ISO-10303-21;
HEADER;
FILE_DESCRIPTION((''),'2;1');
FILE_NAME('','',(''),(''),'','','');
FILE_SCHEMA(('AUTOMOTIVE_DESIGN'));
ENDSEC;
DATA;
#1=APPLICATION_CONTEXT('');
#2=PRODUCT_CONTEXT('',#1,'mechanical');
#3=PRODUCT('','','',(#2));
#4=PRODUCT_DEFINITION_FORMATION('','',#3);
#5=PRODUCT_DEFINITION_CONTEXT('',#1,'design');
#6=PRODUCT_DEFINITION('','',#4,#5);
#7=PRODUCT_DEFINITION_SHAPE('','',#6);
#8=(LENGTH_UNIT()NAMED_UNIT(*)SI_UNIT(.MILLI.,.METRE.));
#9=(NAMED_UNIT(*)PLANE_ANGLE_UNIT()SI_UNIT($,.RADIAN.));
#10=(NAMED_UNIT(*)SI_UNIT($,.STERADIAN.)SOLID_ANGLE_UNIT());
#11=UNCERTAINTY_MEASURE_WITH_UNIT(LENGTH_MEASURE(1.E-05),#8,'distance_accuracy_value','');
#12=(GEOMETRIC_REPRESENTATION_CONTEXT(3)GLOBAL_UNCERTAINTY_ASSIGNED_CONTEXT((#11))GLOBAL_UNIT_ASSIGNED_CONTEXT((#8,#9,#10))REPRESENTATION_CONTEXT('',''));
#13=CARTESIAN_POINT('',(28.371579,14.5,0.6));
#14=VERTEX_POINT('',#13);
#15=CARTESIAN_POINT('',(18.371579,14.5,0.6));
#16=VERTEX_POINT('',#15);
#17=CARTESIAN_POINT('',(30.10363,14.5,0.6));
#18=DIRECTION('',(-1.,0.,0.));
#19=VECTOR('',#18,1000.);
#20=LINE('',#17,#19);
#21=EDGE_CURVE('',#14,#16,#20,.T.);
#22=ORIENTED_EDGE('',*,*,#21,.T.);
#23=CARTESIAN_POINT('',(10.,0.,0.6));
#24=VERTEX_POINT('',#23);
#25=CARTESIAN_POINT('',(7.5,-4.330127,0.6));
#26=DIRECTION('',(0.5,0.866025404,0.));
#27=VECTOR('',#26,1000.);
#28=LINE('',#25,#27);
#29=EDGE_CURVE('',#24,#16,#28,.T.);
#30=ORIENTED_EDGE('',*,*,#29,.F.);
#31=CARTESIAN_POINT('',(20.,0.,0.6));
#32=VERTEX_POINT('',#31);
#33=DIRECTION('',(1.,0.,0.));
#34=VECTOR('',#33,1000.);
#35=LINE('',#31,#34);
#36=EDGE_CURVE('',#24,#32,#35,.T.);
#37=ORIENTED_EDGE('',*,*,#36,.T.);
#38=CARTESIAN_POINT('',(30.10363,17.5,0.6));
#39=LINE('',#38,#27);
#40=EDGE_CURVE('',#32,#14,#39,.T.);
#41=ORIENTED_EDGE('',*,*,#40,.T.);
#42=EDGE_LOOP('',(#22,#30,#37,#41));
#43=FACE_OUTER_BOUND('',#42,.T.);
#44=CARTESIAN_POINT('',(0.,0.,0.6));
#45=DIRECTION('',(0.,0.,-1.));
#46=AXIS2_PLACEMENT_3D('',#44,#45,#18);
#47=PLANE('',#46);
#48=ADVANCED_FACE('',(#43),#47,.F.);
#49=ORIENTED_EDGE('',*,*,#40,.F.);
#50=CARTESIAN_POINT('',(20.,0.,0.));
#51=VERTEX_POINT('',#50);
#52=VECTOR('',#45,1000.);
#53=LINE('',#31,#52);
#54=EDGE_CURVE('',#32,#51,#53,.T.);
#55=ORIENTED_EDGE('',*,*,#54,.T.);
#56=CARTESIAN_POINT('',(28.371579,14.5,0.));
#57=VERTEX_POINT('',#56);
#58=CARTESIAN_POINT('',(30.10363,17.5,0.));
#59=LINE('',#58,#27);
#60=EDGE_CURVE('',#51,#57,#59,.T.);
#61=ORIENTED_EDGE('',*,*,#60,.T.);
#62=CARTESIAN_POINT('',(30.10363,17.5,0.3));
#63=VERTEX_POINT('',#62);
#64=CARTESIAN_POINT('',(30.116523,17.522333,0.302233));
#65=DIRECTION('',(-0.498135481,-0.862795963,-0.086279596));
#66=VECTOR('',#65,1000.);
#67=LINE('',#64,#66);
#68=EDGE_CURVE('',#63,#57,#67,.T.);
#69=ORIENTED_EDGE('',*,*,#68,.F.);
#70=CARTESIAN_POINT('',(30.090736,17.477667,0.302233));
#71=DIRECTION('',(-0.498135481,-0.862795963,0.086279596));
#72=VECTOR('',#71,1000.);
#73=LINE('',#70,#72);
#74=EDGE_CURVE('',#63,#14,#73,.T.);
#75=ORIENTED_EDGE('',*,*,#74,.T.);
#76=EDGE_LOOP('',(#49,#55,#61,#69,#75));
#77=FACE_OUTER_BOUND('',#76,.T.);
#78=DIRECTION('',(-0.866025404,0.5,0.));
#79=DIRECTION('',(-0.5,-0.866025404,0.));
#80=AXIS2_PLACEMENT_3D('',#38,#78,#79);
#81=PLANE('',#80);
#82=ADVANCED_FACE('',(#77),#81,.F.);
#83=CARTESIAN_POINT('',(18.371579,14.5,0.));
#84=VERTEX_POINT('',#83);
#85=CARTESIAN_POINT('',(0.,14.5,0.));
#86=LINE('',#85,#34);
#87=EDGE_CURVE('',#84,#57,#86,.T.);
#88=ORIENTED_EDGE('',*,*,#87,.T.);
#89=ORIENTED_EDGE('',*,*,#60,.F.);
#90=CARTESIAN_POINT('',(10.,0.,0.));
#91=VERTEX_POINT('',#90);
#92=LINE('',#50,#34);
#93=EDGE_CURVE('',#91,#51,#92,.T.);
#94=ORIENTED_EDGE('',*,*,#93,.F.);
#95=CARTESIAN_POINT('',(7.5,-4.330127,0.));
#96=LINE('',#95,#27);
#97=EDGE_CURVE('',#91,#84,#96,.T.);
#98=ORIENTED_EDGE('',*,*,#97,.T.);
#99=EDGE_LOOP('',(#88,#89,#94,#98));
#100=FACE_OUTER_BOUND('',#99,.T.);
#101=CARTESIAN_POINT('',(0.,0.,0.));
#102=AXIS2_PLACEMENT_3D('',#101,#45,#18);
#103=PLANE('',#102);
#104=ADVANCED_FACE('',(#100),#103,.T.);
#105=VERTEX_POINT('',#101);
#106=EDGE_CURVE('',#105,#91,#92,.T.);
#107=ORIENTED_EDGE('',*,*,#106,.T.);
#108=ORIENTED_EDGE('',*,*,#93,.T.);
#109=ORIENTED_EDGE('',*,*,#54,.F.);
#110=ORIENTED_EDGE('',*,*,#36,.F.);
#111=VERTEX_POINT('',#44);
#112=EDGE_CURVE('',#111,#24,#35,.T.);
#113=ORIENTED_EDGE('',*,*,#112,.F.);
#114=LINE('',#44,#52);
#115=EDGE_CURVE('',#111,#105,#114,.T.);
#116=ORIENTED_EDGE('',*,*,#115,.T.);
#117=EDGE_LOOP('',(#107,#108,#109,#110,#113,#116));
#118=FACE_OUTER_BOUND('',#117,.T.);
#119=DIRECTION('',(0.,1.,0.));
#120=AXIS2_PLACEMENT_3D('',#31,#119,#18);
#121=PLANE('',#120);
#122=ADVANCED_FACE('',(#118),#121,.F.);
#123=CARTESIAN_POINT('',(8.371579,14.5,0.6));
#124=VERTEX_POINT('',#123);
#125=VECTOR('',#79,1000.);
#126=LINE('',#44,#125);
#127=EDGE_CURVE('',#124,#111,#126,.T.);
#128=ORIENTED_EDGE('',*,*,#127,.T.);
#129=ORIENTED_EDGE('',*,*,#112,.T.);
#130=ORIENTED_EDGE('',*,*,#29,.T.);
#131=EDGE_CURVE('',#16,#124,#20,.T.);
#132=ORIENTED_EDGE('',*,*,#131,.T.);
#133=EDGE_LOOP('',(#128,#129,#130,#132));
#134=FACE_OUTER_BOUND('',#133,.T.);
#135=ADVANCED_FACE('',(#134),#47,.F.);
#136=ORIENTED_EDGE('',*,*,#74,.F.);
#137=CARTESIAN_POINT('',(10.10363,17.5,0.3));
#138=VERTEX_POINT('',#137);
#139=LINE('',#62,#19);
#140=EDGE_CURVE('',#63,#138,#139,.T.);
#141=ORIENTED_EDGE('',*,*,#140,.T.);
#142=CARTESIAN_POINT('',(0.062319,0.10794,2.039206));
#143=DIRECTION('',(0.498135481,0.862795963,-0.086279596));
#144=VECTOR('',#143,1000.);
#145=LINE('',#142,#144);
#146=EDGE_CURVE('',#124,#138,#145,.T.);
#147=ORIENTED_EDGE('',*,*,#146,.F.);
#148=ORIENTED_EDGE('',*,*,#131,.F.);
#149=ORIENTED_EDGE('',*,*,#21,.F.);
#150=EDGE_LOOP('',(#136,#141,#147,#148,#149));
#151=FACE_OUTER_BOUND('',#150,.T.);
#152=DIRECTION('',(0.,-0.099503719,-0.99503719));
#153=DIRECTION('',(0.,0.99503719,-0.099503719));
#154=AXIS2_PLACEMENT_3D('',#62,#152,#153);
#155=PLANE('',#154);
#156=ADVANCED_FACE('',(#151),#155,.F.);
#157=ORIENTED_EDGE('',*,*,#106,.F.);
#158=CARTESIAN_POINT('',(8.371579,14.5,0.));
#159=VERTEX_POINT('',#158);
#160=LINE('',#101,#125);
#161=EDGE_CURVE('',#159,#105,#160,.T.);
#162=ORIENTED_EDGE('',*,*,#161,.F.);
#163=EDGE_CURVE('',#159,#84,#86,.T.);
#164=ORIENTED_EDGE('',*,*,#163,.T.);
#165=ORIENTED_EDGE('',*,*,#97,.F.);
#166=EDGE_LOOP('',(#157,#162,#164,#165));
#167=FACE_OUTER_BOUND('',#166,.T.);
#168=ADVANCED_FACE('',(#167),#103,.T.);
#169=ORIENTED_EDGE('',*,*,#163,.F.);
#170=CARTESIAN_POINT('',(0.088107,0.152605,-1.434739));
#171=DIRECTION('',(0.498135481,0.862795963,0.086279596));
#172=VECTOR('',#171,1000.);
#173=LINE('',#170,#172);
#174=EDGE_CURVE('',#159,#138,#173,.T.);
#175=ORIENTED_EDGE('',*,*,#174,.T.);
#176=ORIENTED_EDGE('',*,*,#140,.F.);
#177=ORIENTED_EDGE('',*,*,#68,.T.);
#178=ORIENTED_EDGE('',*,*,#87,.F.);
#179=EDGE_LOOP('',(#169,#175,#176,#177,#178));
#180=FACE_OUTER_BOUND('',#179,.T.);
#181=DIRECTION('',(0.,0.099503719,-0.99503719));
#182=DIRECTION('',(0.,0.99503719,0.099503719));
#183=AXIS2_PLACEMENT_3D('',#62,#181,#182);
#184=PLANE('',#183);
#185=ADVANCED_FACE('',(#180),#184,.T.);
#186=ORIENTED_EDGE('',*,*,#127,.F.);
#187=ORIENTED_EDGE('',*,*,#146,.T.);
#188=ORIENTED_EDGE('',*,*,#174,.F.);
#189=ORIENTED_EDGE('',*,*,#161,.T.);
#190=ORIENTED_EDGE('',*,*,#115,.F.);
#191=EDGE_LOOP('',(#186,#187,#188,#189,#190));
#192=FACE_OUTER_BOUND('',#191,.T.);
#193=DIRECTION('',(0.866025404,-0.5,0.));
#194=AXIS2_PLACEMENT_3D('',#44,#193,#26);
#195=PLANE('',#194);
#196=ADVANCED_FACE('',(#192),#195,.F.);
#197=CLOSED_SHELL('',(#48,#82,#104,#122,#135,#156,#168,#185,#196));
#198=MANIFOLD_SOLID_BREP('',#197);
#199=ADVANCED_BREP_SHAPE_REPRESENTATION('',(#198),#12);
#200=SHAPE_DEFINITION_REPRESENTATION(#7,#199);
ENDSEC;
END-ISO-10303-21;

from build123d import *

# Parameters (mm, degrees)
BOSS_EXTRUDE1_DEPTH = 0.6
CUT_EXTRUDE1_DEPTH  = 35.825831243


with BuildPart() as part:
    # Sketch1 → Boss-Extrude1 (new body)
    with BuildSketch(Plane.XY):
        Polygon((0, 0), (10.103629711, 17.5), (30.103629711, 17.5), (20, 0), align=None)
    extrude(amount=BOSS_EXTRUDE1_DEPTH)

    # Sketch2 → Cut-Extrude1 (cut, through all)
    with BuildSketch(Plane(origin=(0, 0, 0), x_dir=(0, 0, -1), z_dir=(1, 0, 0))):
        Polygon((-0.3, 17.5), (0, 14.5), (0, 17.5), align=None)
    cut_extrude1 = extrude(amount=CUT_EXTRUDE1_DEPTH, mode=Mode.SUBTRACT)

    # Mirror1: Cut-Extrude1 across plane
    add(cut_extrude1.mirror(Plane(origin=(0, 0, 0.3), x_dir=(1, 0, 0), z_dir=(0, 0, -1))), mode=Mode.SUBTRACT)


solid = part.part
